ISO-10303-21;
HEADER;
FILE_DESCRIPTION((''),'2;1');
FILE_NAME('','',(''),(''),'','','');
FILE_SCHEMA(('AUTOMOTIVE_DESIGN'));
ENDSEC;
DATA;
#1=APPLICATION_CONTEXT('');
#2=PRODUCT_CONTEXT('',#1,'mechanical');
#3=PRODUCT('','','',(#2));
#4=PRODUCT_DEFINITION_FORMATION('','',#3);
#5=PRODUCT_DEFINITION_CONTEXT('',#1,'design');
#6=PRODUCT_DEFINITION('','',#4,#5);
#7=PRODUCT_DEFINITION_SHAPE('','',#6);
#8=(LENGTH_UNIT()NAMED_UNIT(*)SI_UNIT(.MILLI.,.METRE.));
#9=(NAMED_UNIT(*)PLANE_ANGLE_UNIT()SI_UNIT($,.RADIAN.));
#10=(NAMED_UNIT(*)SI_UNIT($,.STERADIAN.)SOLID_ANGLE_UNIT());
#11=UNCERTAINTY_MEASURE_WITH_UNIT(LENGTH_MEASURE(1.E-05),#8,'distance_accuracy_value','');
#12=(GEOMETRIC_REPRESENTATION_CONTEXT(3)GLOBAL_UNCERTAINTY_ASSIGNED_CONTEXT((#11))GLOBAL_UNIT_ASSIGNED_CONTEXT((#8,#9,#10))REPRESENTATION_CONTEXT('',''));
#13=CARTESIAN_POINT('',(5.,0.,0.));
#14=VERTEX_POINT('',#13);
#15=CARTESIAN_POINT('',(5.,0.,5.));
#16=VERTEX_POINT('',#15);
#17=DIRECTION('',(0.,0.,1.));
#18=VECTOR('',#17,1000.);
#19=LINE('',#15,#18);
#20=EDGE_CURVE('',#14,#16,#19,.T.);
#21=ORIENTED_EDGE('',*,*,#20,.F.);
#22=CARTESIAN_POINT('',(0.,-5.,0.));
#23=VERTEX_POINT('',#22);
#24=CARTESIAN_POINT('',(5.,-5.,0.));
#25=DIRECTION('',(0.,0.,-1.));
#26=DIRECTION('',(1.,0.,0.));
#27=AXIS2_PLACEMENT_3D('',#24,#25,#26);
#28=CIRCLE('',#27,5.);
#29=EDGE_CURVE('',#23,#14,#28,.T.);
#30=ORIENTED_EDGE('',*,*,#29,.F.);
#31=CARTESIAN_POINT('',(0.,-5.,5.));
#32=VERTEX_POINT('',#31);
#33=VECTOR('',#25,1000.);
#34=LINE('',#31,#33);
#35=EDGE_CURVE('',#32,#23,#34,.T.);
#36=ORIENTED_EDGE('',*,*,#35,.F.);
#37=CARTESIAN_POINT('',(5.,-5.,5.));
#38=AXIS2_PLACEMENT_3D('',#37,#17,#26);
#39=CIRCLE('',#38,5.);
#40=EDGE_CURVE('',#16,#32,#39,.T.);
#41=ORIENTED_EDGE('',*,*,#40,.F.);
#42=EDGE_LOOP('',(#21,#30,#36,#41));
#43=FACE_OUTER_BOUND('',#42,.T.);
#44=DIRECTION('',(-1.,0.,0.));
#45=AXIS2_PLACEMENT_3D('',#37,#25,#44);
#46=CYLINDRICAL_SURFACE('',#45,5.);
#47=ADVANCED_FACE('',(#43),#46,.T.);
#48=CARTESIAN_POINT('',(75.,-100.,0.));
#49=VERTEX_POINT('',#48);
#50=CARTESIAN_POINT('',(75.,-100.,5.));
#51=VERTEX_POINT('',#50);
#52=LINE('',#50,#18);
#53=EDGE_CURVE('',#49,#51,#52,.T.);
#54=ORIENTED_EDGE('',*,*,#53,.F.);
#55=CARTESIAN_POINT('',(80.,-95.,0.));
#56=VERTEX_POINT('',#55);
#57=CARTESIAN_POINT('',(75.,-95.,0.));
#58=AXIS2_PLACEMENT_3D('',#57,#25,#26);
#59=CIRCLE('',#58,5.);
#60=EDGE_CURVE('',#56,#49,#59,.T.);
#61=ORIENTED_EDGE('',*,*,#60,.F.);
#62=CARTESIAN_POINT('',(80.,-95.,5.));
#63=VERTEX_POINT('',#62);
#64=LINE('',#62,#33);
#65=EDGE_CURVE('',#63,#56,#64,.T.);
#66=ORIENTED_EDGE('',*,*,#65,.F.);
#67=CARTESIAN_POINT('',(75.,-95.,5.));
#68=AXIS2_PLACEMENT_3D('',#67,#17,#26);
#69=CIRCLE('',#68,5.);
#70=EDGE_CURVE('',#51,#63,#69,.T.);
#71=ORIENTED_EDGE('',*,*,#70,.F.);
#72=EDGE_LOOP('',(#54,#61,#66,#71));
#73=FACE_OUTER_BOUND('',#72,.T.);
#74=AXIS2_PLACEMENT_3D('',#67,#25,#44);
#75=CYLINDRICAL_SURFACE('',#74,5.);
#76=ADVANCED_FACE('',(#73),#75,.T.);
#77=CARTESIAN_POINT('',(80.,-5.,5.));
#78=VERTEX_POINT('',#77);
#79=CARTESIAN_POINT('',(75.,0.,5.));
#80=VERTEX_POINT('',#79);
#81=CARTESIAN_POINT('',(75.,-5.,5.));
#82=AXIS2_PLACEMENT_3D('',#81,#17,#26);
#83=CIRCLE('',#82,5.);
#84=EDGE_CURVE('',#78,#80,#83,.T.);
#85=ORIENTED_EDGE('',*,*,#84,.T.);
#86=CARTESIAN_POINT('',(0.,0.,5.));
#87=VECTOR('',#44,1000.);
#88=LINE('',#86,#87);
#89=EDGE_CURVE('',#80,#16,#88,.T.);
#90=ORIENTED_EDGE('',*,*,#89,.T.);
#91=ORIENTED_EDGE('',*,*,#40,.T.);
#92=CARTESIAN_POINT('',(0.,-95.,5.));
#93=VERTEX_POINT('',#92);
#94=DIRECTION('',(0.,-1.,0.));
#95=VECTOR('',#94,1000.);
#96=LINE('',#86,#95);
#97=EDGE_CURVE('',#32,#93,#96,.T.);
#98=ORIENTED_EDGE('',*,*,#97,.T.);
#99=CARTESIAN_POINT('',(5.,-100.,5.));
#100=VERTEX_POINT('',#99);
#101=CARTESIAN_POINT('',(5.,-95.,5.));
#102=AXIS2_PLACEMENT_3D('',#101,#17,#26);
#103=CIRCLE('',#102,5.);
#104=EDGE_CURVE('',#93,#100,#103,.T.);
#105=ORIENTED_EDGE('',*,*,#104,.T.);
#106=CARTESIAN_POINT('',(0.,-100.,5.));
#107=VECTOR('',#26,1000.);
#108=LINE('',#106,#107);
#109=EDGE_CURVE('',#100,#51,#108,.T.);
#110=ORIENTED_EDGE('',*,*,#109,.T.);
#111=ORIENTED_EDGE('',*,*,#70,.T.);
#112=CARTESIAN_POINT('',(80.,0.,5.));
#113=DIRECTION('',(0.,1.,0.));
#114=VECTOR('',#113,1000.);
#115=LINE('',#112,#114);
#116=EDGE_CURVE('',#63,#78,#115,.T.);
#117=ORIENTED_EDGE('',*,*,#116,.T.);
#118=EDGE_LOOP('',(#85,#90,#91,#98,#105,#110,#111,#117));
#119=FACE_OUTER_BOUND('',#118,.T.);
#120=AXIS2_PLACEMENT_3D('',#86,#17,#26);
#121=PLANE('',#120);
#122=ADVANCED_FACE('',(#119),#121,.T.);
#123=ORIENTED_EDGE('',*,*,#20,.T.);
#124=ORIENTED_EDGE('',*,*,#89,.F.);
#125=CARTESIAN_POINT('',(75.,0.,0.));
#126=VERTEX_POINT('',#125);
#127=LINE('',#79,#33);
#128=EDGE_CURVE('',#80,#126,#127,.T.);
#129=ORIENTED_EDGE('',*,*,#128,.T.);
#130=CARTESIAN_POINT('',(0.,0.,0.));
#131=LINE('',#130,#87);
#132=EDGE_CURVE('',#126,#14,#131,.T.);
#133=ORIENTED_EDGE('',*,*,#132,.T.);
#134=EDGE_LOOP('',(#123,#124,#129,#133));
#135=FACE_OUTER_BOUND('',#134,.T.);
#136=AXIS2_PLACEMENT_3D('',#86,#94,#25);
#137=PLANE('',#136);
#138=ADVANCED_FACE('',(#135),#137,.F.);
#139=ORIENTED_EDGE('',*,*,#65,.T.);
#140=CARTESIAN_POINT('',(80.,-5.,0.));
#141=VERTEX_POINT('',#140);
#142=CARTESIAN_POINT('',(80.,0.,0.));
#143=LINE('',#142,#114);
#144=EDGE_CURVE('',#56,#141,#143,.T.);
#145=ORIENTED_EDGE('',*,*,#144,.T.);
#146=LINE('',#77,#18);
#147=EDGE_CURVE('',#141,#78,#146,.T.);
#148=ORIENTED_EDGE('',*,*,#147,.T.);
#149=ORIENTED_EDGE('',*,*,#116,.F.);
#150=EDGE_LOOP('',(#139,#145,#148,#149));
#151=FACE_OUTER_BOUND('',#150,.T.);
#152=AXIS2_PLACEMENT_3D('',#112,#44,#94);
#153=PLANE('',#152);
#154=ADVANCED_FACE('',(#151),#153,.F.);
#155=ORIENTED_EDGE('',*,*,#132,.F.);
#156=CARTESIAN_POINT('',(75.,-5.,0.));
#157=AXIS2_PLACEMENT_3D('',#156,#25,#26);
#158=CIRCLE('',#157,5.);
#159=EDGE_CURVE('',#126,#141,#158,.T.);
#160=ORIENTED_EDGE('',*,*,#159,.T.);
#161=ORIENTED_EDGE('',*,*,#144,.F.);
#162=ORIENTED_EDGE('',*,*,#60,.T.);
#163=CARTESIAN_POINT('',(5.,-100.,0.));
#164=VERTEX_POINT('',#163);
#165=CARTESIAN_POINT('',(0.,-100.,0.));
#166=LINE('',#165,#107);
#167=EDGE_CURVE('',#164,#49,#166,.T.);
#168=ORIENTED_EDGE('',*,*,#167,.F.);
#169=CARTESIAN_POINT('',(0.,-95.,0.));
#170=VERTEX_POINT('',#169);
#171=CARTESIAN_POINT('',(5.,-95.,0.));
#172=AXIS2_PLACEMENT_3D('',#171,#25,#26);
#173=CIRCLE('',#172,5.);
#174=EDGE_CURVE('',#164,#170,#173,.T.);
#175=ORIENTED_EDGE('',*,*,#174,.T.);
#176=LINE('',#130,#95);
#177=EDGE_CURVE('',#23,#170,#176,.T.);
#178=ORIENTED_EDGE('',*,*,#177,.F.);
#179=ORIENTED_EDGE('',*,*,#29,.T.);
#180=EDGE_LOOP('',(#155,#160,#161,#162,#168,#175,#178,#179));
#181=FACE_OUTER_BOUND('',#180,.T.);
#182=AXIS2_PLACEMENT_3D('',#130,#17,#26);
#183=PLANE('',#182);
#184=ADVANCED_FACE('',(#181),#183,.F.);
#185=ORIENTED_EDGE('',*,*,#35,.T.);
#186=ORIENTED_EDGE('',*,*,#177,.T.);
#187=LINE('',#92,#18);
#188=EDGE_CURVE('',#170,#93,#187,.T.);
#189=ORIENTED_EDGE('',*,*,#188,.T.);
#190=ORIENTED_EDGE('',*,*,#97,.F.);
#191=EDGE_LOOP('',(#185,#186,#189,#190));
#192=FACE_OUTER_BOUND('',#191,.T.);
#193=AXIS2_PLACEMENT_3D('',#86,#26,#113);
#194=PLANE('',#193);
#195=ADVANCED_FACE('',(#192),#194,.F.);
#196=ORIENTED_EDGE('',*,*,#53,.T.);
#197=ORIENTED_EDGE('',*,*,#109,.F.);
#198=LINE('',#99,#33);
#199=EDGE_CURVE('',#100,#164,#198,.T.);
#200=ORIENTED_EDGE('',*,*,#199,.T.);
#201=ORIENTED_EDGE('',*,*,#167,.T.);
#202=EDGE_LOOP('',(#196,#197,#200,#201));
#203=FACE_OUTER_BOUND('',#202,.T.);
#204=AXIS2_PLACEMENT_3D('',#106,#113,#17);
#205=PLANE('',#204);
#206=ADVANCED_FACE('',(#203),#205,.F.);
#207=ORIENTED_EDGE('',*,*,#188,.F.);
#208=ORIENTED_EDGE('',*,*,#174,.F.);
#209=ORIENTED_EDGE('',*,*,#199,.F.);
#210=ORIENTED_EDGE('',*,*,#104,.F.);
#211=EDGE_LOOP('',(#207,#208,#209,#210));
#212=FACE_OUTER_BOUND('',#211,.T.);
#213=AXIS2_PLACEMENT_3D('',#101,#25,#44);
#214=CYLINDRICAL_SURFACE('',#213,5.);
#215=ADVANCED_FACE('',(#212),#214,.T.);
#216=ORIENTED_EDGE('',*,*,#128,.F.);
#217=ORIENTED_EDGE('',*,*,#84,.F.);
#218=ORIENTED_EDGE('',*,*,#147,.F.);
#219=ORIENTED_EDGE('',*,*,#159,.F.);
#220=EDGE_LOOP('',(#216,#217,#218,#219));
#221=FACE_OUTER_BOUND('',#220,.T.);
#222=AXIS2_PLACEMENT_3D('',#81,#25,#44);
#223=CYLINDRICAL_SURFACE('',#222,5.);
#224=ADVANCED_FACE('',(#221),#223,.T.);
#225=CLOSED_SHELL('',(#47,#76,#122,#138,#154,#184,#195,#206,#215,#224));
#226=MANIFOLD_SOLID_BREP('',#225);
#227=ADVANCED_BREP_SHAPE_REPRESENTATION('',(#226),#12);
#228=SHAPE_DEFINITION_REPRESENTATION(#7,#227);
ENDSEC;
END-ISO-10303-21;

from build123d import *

# Parameters (mm, degrees)
SKETCH1_W           = 80
SKETCH1_H           = 100
BOSS_EXTRUDE1_DEPTH = 5
FILLET1_R           = 5


with BuildPart() as part:
    # Sketch1 → Boss-Extrude1 (new body)
    with BuildSketch(Plane.XY):
        with Locations((40, -50)):
            Rectangle(SKETCH1_W, SKETCH1_H)
    extrude(amount=BOSS_EXTRUDE1_DEPTH)

    # Fillet1
    fillet1_edges = [part.edges().sort_by_distance(p)[0] for p in [
        (0, 0, 2.5),
        (80, 0, 2.5),
        (80, -100, 2.5),
        (0, -100, 2.5),
    ]]
    fillet(fillet1_edges, radius=FILLET1_R)


solid = part.part
